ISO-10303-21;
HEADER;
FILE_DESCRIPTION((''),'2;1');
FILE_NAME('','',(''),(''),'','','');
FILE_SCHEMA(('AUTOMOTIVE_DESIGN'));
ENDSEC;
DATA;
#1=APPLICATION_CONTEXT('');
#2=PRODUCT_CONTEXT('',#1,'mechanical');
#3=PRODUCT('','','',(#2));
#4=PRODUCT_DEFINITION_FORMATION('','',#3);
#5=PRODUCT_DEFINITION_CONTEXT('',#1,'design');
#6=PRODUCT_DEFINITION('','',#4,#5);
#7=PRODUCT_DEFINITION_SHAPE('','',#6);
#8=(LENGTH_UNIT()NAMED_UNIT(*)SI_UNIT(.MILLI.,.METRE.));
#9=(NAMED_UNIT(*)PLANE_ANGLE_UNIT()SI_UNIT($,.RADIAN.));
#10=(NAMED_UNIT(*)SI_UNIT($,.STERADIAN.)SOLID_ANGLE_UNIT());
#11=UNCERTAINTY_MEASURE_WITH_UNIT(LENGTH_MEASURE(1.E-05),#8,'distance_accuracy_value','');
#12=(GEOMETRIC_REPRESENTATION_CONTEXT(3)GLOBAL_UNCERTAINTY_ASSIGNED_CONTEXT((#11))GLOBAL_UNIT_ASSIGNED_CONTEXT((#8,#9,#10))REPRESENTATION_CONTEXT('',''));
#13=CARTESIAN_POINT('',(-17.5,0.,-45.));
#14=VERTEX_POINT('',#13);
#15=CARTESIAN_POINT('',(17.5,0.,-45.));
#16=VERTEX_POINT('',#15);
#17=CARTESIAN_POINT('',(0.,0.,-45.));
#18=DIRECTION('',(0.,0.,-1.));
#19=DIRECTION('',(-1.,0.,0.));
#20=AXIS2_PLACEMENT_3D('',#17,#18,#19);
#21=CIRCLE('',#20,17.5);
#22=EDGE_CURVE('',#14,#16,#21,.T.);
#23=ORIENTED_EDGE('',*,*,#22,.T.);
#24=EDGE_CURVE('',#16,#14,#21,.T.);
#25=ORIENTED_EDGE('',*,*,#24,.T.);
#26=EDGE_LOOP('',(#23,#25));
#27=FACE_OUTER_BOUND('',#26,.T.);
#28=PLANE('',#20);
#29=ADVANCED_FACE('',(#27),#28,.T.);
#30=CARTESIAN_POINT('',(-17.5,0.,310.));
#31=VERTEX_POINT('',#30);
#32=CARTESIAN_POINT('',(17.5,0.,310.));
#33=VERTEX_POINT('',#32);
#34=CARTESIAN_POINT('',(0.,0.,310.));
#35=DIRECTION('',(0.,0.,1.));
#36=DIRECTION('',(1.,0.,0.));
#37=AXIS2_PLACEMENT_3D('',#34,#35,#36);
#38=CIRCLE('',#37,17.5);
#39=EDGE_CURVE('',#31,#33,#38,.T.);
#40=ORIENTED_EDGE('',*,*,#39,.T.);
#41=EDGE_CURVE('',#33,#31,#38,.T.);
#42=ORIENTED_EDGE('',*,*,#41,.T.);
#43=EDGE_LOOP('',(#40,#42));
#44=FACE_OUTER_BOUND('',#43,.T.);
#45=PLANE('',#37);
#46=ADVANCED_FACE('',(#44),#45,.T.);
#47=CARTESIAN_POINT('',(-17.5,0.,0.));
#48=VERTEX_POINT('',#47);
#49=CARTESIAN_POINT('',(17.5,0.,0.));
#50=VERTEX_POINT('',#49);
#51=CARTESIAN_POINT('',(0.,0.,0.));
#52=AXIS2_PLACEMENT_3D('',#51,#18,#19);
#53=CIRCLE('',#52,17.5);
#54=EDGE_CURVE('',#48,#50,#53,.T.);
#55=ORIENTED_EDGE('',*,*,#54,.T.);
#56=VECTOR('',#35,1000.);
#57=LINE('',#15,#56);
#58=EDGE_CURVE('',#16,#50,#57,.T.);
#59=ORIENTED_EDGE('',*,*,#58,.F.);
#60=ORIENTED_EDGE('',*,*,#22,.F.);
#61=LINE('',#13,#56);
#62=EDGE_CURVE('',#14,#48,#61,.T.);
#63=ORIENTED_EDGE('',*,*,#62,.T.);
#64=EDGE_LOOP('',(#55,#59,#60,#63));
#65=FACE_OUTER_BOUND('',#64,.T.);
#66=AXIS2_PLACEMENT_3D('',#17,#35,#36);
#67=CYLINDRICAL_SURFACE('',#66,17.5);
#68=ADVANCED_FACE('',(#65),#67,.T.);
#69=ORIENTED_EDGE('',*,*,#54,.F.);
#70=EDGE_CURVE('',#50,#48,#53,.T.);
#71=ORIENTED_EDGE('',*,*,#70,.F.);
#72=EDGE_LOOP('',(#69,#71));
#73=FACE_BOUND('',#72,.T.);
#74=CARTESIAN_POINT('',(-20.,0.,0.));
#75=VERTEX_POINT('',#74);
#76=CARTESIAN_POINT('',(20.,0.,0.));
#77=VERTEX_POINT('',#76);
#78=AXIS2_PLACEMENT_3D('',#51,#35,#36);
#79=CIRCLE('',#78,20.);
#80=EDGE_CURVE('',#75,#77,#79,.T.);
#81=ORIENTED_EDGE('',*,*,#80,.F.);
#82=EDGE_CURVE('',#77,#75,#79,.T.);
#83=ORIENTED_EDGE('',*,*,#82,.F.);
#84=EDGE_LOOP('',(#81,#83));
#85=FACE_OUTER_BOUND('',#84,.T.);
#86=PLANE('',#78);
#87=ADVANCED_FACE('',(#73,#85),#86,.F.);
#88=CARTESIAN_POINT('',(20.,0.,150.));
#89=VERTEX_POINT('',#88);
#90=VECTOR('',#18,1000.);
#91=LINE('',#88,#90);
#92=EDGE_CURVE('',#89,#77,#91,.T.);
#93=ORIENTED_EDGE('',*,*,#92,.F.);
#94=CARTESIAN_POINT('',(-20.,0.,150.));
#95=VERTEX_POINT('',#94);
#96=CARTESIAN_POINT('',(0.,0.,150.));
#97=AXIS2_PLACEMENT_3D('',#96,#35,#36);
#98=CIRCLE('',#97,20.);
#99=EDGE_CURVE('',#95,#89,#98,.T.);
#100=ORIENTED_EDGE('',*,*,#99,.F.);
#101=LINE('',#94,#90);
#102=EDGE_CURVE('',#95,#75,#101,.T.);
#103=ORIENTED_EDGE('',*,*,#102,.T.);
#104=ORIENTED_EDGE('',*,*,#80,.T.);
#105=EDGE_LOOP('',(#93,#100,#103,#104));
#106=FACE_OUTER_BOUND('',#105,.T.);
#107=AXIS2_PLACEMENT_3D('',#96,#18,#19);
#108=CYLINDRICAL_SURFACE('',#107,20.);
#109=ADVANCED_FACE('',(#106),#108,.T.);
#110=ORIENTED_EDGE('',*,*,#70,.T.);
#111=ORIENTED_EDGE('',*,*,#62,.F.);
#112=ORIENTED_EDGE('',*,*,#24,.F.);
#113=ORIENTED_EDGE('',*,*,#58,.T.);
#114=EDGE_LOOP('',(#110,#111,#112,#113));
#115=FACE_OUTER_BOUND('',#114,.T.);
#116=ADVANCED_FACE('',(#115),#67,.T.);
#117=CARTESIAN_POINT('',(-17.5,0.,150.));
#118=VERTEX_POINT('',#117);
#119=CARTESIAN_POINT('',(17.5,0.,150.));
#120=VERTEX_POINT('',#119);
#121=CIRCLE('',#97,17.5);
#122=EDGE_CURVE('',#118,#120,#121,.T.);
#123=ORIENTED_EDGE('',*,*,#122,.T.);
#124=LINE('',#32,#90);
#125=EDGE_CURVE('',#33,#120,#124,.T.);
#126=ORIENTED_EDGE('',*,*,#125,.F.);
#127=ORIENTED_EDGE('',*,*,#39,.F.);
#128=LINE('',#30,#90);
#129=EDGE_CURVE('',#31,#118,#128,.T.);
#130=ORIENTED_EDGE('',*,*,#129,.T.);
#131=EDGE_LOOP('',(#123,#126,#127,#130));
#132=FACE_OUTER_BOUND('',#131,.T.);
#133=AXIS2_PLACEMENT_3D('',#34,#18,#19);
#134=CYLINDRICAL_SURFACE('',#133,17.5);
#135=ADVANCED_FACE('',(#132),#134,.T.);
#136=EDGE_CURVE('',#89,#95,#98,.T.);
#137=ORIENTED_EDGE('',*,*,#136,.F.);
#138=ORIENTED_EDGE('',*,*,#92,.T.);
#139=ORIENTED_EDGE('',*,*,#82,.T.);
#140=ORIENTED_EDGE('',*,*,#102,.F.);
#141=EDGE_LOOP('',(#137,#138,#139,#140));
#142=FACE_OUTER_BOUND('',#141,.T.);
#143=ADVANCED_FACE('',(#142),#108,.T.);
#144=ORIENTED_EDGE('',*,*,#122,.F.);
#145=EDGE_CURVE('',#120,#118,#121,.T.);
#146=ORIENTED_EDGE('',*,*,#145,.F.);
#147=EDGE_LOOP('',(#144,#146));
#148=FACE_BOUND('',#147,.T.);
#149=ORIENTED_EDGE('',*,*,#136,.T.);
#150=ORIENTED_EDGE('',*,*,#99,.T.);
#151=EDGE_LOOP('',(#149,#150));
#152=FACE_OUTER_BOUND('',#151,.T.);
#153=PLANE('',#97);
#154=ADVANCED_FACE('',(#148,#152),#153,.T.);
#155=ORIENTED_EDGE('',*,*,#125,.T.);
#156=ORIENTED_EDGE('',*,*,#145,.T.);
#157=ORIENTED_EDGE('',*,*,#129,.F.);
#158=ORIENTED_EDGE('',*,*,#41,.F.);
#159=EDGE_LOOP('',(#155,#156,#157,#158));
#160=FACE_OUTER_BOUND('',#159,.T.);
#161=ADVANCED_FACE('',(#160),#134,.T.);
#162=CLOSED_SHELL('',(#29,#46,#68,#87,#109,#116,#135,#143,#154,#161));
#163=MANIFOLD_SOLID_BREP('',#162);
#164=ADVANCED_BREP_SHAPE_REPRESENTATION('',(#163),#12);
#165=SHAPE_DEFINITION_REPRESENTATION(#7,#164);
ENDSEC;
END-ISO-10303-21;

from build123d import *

# Parameters (mm, degrees)
SKETCH_1_R      = 20
EXTRUDE_1_DEPTH = 150
SKETCH_2_R      = 17.5
EXTRUDE_2_DEPTH = 160
EXTRUDE_START   = 45
SKETCH_3_R      = 17.5
EXTRUDE_3_DEPTH = 45


with BuildPart() as part:
    # 草图1 → 凸台-拉伸1 (new body)
    with BuildSketch(Plane.XY):
        Circle(SKETCH_1_R)
    extrude(amount=EXTRUDE_1_DEPTH)

    # 草图2 → 凸台-拉伸2 (add)
    with BuildSketch(Plane.XY.offset(150)):
        Circle(SKETCH_2_R)
    extrude(amount=EXTRUDE_2_DEPTH)

    # 草图3 → 凸台-拉伸3 (add)
    with BuildSketch(Plane(origin=(0, 0, 0), x_dir=(-1, 0, 0), z_dir=(0, 0, -1)).offset(EXTRUDE_START)):
        with Locations(Location((0, 0, 0), (0, 0, 180))):
            Circle(SKETCH_3_R)
    extrude(amount=-EXTRUDE_3_DEPTH)


solid = part.part
